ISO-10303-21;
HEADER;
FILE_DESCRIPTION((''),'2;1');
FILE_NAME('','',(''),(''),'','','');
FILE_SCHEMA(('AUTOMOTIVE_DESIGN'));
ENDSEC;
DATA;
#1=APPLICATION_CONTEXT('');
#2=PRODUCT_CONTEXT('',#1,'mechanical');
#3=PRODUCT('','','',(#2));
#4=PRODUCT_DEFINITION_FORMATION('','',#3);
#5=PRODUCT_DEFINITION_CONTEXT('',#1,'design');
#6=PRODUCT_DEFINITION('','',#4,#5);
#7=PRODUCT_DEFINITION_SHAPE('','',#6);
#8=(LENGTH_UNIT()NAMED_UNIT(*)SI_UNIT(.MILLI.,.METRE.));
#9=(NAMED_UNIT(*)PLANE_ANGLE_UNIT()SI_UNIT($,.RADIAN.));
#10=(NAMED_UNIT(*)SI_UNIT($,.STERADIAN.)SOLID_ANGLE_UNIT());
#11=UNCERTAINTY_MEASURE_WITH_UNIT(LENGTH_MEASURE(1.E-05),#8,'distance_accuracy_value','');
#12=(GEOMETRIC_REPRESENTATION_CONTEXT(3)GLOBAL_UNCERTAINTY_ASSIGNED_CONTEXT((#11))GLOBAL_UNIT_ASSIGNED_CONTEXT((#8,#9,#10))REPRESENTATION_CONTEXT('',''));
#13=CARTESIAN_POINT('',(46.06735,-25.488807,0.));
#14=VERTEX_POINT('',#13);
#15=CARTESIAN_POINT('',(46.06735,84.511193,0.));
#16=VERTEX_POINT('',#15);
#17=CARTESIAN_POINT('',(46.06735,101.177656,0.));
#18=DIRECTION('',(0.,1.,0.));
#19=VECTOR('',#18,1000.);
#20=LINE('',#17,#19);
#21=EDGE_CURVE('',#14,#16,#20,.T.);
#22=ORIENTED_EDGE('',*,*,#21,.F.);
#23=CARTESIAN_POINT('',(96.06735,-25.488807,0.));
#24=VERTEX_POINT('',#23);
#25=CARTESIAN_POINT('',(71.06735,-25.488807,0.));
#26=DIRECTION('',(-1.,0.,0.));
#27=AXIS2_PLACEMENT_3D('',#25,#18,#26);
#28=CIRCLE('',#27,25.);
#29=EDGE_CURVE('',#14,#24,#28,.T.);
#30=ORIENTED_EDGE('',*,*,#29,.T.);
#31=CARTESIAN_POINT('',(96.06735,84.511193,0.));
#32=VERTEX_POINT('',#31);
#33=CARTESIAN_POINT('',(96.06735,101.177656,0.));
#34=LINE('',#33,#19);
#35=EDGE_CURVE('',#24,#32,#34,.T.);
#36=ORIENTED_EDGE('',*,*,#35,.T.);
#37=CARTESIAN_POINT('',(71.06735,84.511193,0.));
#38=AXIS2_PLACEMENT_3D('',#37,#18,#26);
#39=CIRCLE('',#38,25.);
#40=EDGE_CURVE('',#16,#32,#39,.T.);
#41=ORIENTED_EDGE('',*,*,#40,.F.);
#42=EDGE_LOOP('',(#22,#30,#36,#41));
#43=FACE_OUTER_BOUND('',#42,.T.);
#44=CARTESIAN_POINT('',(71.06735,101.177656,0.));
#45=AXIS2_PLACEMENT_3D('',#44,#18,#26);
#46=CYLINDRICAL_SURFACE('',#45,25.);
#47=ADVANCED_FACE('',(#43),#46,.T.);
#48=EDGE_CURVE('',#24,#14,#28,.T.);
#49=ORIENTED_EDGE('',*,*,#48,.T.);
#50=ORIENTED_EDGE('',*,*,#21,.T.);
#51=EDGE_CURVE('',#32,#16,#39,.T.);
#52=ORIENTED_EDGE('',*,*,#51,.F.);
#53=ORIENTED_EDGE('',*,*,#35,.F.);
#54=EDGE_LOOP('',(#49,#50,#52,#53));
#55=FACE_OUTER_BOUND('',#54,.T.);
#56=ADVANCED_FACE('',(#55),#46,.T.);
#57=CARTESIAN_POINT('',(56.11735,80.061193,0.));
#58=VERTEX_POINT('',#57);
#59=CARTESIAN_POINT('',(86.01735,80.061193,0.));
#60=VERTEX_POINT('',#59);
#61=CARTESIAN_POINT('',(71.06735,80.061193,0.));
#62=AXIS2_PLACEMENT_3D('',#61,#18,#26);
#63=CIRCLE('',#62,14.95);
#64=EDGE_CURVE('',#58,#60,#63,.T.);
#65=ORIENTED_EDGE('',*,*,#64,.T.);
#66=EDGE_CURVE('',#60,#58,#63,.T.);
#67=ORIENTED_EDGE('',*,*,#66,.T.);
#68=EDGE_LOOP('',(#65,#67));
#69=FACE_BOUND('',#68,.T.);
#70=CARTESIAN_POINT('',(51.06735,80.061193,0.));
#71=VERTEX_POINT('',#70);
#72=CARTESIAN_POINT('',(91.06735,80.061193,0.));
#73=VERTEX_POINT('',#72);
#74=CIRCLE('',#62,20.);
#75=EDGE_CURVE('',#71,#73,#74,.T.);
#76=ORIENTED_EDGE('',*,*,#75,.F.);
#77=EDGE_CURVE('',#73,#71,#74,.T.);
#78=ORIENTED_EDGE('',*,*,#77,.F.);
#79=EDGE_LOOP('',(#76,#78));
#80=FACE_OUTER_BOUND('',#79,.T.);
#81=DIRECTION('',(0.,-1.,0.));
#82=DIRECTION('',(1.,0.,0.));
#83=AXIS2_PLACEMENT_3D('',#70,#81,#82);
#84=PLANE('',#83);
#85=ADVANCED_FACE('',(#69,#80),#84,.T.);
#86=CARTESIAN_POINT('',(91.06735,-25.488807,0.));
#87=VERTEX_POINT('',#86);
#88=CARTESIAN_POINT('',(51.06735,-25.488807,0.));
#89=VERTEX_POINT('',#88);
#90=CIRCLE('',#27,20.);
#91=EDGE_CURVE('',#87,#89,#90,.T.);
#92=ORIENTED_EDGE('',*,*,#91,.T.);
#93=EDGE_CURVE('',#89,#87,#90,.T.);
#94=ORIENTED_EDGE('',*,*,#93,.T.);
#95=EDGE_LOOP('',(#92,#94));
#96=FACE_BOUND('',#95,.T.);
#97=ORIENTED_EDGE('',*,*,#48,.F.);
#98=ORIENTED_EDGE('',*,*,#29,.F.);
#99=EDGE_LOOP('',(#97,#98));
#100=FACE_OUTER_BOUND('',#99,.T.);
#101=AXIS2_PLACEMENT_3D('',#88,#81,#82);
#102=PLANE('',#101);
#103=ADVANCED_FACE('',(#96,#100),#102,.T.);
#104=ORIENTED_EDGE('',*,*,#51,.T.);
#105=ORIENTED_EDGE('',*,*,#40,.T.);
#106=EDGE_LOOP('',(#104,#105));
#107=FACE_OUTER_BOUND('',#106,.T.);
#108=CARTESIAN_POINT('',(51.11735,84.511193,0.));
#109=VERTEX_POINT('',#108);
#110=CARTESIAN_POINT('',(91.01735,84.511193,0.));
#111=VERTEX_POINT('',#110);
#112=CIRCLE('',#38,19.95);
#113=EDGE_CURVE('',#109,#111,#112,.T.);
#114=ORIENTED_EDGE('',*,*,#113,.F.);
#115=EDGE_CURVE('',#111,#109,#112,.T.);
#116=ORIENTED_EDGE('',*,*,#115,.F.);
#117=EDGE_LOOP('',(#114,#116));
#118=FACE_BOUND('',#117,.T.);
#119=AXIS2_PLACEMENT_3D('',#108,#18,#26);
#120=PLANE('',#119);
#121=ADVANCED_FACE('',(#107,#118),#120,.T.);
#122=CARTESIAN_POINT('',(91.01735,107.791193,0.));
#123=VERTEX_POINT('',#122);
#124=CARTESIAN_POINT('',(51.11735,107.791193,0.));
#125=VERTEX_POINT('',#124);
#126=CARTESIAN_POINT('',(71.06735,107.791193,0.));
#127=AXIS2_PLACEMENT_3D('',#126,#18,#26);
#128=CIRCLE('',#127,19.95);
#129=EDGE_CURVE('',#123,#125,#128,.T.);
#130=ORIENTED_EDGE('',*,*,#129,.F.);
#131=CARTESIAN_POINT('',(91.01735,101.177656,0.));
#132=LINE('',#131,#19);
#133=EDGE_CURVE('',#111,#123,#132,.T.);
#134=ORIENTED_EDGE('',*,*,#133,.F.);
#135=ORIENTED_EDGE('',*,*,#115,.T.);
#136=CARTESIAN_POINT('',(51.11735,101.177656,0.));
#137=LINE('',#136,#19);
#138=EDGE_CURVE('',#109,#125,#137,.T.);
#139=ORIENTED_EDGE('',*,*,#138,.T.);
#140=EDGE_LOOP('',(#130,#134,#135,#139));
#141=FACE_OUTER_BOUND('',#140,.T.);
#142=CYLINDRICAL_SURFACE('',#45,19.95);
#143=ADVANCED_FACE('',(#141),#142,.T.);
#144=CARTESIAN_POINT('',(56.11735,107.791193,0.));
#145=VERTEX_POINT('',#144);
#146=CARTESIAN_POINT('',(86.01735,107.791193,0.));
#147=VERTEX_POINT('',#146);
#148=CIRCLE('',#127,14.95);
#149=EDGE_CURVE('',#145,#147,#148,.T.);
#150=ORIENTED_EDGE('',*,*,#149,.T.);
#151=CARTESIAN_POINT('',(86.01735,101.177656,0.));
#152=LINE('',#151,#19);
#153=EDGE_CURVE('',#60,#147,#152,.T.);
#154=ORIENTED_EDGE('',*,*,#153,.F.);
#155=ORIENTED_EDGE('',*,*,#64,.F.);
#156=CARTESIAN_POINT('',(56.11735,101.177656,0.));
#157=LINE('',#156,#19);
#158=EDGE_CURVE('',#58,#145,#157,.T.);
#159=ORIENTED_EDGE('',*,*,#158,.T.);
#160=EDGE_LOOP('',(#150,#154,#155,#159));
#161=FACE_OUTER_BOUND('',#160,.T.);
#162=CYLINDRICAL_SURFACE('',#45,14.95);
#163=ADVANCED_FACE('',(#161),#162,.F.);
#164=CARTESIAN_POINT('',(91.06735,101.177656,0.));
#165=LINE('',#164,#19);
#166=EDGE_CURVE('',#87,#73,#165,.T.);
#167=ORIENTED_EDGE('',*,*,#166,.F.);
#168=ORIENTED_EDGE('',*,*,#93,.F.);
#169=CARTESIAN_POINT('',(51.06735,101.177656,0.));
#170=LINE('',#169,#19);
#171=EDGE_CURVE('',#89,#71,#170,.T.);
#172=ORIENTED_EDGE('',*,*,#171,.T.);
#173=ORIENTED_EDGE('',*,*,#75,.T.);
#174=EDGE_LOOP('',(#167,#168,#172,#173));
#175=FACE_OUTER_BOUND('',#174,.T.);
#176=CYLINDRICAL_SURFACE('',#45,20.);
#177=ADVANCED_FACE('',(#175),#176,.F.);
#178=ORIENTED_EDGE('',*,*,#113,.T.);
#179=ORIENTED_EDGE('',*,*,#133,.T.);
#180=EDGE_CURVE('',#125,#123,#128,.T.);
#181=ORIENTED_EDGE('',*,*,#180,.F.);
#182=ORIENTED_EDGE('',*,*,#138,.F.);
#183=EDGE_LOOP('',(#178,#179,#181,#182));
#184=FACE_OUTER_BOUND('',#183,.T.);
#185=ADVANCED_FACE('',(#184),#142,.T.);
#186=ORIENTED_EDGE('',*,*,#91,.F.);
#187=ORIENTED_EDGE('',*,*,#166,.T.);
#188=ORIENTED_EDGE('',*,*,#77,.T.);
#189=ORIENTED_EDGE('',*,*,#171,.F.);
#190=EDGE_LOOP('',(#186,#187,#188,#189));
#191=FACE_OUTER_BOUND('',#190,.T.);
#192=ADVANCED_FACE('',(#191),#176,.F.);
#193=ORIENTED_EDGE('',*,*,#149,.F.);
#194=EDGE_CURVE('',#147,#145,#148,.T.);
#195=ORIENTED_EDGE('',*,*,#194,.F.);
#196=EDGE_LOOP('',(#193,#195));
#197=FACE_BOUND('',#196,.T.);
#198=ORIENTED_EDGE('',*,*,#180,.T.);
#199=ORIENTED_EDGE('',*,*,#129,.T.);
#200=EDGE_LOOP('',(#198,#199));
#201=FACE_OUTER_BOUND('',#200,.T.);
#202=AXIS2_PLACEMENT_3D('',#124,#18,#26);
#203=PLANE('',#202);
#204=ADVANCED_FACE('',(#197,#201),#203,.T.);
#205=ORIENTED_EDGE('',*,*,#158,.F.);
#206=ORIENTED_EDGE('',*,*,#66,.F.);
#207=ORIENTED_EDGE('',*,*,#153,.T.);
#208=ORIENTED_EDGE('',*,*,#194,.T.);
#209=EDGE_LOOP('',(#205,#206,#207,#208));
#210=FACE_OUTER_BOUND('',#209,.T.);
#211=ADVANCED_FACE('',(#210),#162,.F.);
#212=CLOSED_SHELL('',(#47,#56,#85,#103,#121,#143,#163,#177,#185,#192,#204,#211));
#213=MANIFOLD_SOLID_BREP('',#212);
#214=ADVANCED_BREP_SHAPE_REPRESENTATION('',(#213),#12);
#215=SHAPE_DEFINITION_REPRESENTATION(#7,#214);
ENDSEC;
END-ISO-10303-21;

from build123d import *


with BuildPart() as part:
    # Sketch2 → Revolve1 (revolve)
    with BuildSketch(Plane.XY):
        Polygon((51.067350004, -25.488807327), (51.067350004, 80.061192673), (56.117350004, 80.061192673), (56.117350004, 107.791192673), (51.117350004, 107.791192673), (51.117350004, 97.791192673), (51.117350004, 84.511192673), (46.067350004, 84.511192673), (46.067350004, -25.488807327), align=None)
    revolve(axis=Axis((71.067350004, 101.177656429, 0), (0, -1, 0)))


solid = part.part
